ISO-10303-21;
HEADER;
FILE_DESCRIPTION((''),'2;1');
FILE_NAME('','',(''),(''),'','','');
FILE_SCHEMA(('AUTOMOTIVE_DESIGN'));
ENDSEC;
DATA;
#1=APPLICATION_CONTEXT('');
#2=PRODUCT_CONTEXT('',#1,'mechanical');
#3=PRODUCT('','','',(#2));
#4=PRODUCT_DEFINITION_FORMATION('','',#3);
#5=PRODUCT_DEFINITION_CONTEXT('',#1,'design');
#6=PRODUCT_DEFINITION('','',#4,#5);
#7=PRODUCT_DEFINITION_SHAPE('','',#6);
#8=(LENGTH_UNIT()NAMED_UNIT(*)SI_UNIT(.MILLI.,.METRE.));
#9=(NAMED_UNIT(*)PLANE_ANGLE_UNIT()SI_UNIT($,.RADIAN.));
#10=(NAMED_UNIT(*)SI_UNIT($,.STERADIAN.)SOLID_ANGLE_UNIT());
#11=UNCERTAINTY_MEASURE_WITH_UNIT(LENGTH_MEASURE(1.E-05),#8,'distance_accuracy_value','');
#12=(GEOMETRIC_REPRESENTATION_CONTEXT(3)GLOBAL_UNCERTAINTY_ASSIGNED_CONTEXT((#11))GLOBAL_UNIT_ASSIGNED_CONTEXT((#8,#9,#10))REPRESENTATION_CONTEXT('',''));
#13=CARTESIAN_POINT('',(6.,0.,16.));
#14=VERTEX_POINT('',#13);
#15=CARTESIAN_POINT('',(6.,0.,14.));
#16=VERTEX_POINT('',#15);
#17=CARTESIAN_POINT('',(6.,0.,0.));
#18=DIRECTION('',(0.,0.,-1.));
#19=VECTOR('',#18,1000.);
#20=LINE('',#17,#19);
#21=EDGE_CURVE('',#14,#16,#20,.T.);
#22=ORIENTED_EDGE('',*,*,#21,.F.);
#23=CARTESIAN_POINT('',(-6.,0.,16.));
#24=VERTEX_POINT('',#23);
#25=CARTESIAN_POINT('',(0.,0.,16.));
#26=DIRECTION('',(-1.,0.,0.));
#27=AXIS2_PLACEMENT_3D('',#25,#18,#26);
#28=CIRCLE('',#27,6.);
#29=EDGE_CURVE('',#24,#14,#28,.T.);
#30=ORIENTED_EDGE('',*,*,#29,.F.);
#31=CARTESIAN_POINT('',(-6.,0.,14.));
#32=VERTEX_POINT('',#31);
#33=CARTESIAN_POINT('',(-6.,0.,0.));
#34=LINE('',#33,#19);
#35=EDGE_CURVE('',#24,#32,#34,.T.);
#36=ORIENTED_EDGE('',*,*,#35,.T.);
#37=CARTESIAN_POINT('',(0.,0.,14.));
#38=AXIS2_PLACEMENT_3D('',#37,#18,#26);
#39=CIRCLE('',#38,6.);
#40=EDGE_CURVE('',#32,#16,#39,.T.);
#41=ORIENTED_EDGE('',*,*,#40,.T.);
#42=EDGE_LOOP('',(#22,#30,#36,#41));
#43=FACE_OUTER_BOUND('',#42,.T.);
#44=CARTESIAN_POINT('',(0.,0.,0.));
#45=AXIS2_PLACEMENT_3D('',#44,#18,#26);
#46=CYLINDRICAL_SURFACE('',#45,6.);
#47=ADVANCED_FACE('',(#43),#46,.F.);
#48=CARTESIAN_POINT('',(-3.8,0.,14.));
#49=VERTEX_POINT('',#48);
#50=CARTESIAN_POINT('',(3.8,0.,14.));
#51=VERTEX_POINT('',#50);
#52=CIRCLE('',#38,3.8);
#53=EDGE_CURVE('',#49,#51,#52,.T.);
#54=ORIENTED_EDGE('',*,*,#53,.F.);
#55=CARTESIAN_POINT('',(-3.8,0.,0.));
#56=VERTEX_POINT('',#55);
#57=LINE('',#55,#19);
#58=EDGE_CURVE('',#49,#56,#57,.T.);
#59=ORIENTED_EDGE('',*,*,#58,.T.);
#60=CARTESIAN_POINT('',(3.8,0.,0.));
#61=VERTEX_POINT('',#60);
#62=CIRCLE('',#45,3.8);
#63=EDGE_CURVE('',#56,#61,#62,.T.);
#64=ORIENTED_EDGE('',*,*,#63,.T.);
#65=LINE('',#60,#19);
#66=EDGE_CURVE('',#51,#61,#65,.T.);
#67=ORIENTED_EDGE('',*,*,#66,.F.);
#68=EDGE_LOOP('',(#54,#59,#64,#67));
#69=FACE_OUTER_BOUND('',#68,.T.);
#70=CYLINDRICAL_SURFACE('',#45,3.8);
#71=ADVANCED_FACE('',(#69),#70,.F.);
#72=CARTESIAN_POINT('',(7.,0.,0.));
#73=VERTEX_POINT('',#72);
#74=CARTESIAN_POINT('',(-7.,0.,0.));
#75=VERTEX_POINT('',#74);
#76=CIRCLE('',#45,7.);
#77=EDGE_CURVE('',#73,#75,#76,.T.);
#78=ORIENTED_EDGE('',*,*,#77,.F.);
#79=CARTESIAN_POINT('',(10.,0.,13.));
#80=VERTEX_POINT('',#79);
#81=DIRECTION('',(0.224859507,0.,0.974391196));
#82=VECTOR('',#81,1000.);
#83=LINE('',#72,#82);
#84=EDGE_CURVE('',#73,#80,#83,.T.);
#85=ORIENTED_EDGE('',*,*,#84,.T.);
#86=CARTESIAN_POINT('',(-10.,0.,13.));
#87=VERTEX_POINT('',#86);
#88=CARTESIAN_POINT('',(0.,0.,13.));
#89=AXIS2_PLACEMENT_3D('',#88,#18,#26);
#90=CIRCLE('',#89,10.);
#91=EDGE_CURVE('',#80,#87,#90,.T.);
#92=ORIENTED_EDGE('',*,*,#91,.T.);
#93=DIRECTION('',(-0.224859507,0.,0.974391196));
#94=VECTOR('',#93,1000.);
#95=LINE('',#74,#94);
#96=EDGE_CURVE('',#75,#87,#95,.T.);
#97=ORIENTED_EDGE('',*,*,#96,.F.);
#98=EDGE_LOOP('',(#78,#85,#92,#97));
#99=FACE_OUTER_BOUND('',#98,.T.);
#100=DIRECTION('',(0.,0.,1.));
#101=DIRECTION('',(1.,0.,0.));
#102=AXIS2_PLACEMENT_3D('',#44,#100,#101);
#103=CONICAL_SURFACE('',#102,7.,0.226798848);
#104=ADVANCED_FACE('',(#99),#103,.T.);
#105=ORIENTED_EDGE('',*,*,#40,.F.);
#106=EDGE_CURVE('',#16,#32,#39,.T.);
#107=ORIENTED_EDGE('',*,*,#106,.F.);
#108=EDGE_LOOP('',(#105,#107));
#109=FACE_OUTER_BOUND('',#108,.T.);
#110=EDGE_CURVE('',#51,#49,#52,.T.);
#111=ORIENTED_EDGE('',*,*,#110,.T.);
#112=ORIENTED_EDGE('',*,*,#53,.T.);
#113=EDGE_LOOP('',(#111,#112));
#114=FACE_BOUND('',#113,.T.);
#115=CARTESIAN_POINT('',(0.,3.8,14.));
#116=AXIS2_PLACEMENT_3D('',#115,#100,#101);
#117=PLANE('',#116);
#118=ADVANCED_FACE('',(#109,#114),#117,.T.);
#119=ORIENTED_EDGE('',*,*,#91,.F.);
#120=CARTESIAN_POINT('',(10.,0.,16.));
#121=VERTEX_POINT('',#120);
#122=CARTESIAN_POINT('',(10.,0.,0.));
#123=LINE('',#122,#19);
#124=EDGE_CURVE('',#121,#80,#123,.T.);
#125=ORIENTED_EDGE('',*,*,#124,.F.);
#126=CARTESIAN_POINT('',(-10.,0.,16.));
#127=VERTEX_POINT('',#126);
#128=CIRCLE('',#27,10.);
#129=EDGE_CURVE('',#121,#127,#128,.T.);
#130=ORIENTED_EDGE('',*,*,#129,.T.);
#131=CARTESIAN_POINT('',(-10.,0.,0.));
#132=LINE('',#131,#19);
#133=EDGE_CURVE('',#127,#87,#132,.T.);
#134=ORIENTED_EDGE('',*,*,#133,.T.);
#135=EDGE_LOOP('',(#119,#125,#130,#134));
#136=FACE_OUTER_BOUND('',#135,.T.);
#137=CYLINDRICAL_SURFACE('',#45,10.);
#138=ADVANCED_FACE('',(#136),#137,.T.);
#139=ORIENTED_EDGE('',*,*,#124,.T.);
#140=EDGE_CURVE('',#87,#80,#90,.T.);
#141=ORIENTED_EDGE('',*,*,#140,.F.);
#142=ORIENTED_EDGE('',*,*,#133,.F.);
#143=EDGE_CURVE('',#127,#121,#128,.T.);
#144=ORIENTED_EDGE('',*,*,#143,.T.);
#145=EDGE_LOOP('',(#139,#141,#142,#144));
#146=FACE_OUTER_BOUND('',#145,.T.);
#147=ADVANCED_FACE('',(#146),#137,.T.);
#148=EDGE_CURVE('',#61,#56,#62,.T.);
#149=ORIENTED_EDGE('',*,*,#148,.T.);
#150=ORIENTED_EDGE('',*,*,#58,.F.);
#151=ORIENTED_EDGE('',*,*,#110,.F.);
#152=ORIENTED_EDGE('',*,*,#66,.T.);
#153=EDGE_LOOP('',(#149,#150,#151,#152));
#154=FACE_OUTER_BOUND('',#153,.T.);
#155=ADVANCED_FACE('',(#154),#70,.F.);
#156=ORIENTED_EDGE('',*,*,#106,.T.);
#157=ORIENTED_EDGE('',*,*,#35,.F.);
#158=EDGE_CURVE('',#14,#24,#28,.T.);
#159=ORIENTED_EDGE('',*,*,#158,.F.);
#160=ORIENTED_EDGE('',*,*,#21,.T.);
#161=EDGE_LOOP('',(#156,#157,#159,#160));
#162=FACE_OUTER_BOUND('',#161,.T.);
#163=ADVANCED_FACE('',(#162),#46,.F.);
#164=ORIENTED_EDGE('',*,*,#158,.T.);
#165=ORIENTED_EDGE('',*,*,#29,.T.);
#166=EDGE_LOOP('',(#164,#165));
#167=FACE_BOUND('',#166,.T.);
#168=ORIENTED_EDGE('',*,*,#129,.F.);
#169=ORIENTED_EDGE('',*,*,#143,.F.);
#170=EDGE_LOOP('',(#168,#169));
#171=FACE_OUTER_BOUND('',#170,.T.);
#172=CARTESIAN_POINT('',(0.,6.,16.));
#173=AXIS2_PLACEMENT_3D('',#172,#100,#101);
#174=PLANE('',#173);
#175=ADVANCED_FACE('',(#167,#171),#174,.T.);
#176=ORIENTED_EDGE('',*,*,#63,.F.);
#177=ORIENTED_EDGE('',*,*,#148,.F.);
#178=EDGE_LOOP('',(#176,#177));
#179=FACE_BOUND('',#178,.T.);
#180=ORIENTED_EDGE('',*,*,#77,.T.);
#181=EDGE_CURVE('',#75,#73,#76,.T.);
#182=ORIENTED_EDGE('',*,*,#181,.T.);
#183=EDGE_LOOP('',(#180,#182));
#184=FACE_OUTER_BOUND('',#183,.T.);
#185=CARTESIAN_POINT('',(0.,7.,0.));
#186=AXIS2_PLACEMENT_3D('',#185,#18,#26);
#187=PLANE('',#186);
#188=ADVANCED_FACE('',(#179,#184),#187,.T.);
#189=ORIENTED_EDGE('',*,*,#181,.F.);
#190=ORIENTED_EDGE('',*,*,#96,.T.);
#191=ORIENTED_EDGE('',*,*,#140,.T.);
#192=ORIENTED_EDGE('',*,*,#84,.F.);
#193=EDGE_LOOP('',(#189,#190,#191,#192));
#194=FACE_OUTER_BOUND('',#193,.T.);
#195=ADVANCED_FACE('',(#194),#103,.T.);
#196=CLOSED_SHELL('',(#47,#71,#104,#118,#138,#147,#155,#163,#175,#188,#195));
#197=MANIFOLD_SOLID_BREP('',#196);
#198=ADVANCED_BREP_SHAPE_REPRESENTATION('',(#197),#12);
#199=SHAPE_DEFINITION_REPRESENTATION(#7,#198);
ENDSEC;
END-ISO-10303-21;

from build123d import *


with BuildPart() as part:
    # Bushing Profile Sketch → Bushing Body Revolve (revolve)
    with BuildSketch(Plane(origin=(0, 0, 0), x_dir=(0, 0, -1), z_dir=(1, 0, 0)), mode=Mode.PRIVATE) as bushing_body_revolve_sk:
        Polygon((0, 3.8), (-14, 3.8), (-14, 6), (-16, 6), (-16, 10), (-13, 10), (0, 7), align=None)
    revolve(bushing_body_revolve_sk.sketch.rotate(Axis((0, 0, 0), (0, 0, 1)), 90), axis=Axis((0, 0, 0), (0, 0, 1)))


solid = part.part
